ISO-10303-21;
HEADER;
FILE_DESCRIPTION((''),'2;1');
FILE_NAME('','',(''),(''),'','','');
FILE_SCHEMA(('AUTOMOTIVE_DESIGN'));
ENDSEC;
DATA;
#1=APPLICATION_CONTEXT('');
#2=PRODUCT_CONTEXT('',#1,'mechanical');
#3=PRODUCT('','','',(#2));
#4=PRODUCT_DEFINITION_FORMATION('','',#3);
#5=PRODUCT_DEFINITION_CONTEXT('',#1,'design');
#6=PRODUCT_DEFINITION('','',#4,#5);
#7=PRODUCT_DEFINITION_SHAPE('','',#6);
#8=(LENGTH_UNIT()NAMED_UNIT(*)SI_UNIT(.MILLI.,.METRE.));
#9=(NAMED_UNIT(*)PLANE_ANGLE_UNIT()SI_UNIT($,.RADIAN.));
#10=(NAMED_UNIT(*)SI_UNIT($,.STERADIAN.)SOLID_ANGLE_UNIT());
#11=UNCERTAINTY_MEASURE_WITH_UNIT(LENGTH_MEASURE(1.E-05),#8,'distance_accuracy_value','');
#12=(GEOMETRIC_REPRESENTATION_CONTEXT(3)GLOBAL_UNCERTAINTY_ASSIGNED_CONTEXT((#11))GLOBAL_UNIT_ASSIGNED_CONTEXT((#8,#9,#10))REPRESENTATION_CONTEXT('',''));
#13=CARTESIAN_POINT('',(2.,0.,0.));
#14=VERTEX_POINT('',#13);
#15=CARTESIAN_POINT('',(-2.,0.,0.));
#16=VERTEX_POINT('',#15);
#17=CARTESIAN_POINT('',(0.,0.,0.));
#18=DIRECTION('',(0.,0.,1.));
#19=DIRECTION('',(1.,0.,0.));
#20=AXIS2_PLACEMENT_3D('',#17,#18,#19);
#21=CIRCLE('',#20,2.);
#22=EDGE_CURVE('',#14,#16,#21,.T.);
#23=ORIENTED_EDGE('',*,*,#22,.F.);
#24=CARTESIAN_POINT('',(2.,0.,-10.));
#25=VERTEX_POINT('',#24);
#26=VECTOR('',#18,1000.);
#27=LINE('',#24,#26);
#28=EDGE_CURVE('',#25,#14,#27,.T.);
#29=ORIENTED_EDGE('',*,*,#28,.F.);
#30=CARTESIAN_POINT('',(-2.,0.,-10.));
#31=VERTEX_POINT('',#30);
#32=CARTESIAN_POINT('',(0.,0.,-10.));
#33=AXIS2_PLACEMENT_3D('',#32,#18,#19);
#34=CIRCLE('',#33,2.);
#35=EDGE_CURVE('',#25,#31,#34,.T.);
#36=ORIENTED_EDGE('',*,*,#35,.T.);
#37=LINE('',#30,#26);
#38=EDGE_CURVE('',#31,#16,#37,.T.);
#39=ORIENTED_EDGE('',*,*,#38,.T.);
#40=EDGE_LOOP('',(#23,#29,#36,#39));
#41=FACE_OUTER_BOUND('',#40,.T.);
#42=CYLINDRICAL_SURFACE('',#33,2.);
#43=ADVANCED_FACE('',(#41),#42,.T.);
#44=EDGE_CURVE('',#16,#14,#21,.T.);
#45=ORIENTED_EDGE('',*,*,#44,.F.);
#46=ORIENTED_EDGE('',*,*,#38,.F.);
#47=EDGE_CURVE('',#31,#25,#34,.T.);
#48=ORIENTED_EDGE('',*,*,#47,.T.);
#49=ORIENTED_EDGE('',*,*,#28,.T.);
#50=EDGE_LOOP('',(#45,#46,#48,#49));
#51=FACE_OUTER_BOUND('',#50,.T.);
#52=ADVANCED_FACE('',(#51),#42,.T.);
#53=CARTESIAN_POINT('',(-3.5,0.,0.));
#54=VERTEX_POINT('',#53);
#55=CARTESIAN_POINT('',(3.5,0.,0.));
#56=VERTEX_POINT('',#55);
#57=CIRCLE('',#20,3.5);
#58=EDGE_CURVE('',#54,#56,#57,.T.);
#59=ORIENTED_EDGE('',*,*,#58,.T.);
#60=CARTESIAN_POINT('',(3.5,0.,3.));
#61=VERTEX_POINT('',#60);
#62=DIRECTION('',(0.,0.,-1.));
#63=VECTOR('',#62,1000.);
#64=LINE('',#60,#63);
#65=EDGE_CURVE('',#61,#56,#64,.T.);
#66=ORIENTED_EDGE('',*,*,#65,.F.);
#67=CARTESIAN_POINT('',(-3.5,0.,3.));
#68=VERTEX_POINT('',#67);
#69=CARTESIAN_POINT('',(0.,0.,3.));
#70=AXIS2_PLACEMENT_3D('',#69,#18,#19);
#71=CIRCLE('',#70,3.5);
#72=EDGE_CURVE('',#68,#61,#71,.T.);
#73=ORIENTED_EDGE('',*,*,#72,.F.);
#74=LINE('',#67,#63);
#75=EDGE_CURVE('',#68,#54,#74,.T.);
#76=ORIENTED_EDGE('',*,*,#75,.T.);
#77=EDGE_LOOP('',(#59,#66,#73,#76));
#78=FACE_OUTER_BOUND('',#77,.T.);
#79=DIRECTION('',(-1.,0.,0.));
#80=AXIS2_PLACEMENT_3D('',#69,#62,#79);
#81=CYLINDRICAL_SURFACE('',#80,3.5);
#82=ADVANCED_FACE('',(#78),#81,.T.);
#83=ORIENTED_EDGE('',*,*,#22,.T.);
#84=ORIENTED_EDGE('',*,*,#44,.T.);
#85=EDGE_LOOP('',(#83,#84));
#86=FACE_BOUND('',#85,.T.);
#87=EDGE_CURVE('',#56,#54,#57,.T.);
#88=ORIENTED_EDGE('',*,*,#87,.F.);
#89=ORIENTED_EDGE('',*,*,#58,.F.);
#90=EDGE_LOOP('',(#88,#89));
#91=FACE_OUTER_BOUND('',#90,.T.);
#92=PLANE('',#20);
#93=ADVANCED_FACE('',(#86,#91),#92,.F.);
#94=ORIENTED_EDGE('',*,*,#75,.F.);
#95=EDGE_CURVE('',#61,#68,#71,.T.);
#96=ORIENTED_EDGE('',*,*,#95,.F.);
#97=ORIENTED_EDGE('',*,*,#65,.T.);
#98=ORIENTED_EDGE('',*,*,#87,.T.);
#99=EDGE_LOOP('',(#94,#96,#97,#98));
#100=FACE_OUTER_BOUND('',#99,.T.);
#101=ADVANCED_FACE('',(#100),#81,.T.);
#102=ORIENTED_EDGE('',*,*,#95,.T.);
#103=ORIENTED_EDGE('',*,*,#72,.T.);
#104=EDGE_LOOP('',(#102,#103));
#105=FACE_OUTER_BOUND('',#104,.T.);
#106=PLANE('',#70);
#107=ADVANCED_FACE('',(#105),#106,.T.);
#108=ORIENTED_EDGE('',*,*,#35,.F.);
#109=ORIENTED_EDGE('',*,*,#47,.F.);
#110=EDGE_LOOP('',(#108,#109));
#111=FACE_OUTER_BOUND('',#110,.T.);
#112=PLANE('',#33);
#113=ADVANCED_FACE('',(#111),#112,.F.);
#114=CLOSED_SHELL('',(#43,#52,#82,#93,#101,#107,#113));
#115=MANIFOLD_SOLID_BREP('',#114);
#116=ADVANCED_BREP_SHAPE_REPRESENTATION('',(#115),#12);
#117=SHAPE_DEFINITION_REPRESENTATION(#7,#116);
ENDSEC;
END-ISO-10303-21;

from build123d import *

# Parameters (mm, degrees)
SKETCH_1_R      = 2
EXTRUDE_1_DEPTH = 10
SKETCH_2_R      = 3.5
EXTRUDE_2_DEPTH = 3


with BuildPart() as part:
    # 草图1 → 凸台-拉伸1 (new body)
    with BuildSketch(Plane.XY):
        Circle(SKETCH_1_R)
    extrude(amount=-EXTRUDE_1_DEPTH)

    # 草图2 → 凸台-拉伸2 (add)
    with BuildSketch(Plane.XY):
        Circle(SKETCH_2_R)
    extrude(amount=EXTRUDE_2_DEPTH)


solid = part.part
